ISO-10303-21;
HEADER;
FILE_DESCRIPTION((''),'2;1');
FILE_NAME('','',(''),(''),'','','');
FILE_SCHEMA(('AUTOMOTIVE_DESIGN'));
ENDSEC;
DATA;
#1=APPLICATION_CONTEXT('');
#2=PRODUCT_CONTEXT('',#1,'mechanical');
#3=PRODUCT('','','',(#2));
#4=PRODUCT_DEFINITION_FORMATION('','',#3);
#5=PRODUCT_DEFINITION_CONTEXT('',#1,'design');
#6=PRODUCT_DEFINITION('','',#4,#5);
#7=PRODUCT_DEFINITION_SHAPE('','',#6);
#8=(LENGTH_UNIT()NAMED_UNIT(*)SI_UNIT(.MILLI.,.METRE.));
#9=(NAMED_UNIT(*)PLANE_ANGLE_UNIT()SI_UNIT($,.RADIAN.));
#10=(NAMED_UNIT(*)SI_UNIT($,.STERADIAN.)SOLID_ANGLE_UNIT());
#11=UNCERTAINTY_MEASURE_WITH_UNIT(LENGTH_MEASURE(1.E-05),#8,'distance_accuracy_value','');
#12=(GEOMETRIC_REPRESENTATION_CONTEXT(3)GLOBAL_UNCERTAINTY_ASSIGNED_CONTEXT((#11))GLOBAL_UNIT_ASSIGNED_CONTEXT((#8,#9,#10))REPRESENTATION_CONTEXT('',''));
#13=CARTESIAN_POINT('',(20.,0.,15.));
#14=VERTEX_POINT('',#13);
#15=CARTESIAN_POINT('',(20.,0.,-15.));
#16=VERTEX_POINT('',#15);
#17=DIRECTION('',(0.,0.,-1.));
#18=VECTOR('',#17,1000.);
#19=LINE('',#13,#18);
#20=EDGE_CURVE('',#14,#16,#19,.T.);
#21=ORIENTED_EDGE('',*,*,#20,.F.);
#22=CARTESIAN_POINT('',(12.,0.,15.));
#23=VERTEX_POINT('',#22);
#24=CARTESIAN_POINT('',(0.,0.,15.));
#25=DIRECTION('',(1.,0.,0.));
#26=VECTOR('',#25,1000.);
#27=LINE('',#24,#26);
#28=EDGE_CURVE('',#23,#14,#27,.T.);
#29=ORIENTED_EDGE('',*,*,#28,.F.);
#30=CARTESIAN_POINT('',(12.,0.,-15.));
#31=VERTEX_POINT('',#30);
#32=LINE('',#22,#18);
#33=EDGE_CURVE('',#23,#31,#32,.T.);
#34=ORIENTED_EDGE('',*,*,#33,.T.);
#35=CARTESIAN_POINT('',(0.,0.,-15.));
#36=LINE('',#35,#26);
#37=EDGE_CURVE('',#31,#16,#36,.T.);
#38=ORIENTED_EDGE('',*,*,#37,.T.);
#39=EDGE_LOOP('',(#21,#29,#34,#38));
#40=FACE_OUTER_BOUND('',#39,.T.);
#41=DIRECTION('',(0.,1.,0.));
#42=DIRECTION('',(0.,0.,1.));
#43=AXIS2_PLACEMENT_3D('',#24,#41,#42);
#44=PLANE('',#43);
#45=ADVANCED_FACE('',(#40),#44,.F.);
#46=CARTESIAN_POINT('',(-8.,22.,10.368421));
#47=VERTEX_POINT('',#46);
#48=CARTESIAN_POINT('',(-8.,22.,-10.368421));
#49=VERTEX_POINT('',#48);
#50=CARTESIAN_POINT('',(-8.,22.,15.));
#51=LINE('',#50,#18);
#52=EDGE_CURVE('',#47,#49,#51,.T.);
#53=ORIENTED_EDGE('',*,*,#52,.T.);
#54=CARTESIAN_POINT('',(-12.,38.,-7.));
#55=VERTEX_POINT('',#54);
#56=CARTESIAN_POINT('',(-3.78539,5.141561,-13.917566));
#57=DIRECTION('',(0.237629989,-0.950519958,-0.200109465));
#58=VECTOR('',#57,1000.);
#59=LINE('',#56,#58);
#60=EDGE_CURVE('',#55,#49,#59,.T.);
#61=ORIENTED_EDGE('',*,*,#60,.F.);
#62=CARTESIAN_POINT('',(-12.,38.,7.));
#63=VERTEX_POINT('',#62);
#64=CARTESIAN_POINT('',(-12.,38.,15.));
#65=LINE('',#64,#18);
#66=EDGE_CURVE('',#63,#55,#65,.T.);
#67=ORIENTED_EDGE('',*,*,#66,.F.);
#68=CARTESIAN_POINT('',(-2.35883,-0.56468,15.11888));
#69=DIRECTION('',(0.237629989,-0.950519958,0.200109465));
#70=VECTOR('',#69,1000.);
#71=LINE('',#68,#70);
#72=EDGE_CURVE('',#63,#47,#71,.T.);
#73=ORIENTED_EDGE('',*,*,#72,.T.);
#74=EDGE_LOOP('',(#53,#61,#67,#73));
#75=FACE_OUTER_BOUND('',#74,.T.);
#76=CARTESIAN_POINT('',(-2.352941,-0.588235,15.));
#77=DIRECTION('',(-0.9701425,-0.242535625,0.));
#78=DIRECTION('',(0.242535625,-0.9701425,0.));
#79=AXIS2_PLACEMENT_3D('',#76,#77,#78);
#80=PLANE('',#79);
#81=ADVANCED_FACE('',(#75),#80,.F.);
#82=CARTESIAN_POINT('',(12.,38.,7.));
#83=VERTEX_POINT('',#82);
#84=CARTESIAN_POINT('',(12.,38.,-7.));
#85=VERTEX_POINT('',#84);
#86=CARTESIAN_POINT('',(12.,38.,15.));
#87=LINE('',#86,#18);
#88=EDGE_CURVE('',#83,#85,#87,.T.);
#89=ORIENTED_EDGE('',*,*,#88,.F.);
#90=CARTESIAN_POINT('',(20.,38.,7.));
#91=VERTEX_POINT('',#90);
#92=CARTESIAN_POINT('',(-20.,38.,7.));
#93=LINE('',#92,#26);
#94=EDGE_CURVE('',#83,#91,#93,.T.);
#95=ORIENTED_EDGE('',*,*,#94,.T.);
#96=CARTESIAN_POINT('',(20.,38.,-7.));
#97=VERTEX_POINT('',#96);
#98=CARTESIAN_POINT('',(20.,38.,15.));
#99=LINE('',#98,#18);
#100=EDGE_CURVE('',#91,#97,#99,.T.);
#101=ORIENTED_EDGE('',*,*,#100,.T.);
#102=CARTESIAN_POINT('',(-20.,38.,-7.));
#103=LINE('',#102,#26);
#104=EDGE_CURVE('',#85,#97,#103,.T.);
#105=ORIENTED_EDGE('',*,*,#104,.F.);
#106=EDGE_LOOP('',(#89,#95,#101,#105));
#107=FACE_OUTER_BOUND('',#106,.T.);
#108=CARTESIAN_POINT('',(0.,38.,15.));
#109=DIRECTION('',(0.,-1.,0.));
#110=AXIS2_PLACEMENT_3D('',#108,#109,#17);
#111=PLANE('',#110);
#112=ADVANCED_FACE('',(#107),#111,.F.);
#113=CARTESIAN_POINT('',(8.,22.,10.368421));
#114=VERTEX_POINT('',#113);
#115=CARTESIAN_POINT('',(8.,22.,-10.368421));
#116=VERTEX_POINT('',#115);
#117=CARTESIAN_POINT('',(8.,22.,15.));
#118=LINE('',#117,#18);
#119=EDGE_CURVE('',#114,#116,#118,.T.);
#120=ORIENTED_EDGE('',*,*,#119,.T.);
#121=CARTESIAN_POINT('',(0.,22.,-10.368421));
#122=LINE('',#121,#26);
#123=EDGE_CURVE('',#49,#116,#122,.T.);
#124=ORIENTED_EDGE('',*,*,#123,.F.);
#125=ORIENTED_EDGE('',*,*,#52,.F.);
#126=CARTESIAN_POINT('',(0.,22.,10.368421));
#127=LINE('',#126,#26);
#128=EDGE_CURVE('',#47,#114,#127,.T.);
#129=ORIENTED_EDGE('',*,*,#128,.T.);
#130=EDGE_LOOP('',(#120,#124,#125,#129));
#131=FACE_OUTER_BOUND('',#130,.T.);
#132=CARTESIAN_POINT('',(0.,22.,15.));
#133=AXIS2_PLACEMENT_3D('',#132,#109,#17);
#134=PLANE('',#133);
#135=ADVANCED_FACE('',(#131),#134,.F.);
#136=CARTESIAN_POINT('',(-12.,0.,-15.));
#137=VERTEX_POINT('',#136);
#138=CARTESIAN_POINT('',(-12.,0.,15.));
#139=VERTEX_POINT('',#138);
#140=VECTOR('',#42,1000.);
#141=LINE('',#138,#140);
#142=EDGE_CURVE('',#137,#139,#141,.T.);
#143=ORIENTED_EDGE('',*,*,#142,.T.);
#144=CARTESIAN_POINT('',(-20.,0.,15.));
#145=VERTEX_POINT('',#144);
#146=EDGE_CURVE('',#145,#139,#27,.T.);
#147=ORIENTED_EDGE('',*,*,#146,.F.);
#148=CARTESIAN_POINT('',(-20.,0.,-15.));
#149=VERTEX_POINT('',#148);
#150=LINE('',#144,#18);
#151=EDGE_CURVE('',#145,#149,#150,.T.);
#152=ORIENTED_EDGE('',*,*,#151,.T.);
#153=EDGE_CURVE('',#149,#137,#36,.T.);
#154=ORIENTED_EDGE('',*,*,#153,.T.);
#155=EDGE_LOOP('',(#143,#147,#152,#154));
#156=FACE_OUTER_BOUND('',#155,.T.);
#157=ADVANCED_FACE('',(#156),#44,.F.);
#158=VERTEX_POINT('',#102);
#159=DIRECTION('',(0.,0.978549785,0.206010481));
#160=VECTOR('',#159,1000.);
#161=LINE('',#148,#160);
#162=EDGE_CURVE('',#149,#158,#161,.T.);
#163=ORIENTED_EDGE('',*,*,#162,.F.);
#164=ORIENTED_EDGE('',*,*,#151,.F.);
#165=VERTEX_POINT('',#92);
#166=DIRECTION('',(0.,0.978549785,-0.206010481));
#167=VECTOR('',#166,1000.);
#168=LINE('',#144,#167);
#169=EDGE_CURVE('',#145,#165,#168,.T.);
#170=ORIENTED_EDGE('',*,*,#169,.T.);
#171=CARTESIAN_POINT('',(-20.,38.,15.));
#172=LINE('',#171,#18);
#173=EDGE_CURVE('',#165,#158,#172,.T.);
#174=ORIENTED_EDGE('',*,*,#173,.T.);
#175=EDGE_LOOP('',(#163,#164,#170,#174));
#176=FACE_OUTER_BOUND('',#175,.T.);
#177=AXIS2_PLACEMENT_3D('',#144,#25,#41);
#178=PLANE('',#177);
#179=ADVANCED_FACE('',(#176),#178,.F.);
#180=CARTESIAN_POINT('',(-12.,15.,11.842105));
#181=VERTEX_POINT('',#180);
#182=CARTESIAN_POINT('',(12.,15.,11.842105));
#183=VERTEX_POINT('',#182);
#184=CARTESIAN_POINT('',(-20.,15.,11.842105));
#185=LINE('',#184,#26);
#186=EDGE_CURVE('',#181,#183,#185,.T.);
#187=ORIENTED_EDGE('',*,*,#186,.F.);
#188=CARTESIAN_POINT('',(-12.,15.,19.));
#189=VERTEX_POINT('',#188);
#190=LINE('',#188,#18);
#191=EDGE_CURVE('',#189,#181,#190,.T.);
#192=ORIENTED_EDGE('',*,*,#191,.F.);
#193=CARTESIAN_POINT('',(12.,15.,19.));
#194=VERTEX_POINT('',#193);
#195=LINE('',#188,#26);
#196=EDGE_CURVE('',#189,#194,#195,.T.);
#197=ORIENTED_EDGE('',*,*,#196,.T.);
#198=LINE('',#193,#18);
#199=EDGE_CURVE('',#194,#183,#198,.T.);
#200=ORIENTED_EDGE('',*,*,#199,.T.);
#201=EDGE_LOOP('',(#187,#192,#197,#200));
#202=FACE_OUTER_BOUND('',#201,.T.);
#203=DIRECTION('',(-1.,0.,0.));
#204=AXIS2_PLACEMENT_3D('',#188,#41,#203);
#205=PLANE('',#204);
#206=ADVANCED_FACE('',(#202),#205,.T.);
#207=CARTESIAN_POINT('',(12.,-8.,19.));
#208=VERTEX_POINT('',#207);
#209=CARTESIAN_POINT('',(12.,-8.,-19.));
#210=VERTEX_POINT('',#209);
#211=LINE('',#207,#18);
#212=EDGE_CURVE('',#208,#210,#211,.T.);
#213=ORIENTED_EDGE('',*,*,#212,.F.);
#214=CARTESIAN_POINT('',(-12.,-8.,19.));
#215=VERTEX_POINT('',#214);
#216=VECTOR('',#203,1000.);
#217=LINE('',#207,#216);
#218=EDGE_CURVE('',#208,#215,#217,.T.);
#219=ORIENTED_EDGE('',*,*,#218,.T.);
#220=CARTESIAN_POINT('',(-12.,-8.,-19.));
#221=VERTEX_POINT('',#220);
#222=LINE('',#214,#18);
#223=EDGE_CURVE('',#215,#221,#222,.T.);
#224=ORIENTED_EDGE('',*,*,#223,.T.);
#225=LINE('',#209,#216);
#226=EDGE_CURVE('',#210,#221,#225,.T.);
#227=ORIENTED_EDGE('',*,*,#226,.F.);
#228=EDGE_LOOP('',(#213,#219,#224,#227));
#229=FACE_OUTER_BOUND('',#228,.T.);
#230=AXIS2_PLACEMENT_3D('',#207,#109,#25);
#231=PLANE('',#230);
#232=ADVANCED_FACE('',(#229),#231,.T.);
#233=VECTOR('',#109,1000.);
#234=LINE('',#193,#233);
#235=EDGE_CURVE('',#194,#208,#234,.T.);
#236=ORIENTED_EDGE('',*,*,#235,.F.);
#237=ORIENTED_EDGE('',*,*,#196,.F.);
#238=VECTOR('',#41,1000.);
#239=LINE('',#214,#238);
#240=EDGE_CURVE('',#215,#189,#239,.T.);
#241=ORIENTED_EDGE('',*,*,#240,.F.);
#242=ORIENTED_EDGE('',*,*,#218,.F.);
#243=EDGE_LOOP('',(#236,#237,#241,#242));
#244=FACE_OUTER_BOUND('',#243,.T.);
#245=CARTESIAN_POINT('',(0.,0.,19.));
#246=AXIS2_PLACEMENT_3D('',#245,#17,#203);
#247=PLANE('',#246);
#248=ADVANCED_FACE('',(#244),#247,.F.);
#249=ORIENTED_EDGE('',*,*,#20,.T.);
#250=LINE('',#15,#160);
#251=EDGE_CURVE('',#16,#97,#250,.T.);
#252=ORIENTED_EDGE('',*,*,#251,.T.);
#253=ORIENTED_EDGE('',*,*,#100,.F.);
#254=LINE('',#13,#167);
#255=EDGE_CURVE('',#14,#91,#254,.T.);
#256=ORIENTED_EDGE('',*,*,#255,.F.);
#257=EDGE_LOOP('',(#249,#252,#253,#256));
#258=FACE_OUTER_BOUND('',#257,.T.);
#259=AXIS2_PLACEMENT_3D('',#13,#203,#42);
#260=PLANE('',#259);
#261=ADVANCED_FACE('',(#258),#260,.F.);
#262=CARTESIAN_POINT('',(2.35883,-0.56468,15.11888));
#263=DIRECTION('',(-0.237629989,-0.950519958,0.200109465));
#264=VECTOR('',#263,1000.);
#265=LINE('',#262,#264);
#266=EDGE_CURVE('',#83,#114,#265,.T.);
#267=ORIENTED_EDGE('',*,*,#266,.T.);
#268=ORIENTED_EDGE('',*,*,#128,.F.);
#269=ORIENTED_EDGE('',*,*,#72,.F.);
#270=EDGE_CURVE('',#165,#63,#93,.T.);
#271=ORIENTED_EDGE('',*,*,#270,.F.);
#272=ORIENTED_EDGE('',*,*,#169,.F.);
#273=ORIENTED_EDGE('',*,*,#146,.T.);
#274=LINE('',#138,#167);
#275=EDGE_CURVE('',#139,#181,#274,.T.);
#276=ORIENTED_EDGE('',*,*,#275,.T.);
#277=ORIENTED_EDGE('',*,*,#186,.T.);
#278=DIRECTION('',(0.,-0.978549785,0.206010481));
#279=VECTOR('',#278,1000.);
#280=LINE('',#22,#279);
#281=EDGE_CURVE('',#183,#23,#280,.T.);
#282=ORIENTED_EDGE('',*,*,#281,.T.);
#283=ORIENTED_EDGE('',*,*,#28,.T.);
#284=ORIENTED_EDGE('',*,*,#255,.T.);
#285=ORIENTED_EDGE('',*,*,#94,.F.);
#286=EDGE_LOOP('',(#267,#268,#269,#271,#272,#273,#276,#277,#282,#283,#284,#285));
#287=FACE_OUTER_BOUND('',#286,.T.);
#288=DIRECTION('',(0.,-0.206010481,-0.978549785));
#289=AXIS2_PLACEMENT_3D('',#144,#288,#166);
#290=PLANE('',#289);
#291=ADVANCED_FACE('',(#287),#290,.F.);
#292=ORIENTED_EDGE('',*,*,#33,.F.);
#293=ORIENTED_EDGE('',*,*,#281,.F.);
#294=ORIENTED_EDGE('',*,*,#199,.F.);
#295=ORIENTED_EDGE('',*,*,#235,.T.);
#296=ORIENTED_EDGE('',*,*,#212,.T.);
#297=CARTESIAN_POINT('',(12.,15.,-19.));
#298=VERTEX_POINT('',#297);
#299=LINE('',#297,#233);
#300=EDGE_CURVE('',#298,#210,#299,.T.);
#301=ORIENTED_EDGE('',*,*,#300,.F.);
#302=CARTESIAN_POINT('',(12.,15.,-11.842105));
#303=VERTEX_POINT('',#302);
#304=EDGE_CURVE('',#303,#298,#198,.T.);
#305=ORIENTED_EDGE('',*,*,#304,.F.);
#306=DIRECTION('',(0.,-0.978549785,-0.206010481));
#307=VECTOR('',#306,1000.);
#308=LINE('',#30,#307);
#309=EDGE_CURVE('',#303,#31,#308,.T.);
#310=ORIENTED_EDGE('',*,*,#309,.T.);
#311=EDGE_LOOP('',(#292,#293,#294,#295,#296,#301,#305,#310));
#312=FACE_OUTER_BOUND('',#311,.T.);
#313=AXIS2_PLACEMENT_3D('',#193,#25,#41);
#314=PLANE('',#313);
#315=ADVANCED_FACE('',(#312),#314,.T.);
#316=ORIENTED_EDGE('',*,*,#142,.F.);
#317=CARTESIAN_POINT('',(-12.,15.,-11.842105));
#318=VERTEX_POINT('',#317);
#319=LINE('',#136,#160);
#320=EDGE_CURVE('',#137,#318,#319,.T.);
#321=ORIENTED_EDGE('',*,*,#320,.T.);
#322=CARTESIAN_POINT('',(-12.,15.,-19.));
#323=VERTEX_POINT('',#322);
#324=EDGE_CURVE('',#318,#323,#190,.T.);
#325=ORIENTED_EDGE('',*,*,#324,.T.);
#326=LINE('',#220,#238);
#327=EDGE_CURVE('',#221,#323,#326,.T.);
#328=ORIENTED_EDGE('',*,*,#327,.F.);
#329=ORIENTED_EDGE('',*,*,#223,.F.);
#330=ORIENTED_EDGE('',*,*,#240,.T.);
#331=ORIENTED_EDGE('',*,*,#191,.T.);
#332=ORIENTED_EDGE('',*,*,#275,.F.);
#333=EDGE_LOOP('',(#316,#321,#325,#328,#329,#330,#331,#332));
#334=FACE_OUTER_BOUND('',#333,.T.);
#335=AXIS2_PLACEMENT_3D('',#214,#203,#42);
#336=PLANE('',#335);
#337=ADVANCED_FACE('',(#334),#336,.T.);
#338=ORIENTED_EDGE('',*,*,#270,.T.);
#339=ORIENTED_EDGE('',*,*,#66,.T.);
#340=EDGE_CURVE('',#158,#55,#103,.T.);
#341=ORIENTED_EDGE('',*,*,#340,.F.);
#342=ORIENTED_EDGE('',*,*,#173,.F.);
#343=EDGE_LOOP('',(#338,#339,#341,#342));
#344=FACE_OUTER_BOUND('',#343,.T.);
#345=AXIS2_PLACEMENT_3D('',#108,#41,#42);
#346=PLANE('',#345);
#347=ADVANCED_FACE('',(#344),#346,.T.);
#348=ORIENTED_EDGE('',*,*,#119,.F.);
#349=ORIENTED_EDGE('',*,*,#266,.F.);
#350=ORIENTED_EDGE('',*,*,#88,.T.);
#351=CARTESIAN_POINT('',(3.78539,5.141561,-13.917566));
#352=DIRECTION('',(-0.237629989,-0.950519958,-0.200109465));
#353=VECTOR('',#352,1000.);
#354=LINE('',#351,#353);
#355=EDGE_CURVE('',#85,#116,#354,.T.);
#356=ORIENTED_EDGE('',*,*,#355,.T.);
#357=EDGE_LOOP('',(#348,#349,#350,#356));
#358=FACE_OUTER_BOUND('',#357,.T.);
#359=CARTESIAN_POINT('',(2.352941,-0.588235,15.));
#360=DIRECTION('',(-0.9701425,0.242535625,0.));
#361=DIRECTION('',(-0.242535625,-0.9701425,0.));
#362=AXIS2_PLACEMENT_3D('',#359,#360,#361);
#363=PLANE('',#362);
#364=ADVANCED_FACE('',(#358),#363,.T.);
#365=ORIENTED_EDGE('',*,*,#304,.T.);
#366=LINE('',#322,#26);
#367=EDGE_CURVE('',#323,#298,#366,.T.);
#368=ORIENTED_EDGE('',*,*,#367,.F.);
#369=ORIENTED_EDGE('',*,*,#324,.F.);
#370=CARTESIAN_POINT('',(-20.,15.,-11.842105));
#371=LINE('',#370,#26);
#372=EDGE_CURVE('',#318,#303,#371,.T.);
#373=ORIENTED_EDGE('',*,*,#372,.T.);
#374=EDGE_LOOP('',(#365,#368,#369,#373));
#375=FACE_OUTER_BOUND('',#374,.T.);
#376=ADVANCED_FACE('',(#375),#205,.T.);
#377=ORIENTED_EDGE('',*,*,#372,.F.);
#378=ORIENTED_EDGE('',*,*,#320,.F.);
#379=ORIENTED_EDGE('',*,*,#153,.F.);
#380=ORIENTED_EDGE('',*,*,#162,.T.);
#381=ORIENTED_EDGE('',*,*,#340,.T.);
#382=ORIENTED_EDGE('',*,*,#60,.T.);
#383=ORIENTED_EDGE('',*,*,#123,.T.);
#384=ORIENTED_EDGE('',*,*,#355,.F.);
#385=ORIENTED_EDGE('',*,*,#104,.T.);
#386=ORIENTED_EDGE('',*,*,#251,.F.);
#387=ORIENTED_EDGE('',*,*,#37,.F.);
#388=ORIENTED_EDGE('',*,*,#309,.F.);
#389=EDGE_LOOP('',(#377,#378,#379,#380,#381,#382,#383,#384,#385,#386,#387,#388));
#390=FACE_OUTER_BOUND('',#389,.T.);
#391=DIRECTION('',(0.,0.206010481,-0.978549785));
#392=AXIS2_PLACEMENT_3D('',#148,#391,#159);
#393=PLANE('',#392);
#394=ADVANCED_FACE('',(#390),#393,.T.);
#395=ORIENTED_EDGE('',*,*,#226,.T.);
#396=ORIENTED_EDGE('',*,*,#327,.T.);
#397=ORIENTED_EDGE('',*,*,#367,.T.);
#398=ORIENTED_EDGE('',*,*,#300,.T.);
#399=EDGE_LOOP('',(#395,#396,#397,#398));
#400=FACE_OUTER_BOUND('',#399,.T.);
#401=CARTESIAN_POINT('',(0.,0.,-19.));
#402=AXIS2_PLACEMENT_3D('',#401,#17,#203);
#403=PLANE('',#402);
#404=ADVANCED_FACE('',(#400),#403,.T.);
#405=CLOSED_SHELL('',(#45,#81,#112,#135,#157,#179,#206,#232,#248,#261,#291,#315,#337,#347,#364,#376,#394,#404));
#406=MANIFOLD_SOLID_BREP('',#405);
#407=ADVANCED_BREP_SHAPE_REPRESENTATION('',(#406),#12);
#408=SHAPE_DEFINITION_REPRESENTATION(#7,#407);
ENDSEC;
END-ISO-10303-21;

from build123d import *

# Parameters (mm, degrees)
BASE_BLOCK_30MM_DEPTH  = 15
GROOVE_CUT_40MM_DEPTH  = 20
FRONT_BLOCK_SKETCH_W   = 24
FRONT_BLOCK_SKETCH_H   = 23
FRONT_BLOCK_38MM_DEPTH = 19


with BuildPart() as part:
    # Base Profile Sketch → Base Block 30mm (new, symmetric)
    with BuildSketch(Plane.XY):
        Polygon((8, 22), (12, 38), (20, 38), (20, 0), (0, 0), (-20, 0), (-20, 38), (-12, 38), (-8, 22), align=None)
    extrude(amount=BASE_BLOCK_30MM_DEPTH, both=True)

    # Groove Profile Sketch → Groove Cut 40mm (cut, symmetric)
    with BuildSketch(Plane(origin=(0, 0, 0), x_dir=(0, 0, -1), z_dir=(1, 0, 0))):
        Polygon((-15, 0), (-7, 38), (-15, 38), align=None)
        Polygon((15, 38), (15, 0), (7, 38), align=None)
    extrude(amount=GROOVE_CUT_40MM_DEPTH, both=True, mode=Mode.SUBTRACT)

    # Front Block Sketch → Front Block 38mm (add, symmetric)
    with BuildSketch(Plane.XY):
        with Locations((0, 3.5)):
            Rectangle(FRONT_BLOCK_SKETCH_W, FRONT_BLOCK_SKETCH_H)
    extrude(amount=FRONT_BLOCK_38MM_DEPTH, both=True)


solid = part.part
